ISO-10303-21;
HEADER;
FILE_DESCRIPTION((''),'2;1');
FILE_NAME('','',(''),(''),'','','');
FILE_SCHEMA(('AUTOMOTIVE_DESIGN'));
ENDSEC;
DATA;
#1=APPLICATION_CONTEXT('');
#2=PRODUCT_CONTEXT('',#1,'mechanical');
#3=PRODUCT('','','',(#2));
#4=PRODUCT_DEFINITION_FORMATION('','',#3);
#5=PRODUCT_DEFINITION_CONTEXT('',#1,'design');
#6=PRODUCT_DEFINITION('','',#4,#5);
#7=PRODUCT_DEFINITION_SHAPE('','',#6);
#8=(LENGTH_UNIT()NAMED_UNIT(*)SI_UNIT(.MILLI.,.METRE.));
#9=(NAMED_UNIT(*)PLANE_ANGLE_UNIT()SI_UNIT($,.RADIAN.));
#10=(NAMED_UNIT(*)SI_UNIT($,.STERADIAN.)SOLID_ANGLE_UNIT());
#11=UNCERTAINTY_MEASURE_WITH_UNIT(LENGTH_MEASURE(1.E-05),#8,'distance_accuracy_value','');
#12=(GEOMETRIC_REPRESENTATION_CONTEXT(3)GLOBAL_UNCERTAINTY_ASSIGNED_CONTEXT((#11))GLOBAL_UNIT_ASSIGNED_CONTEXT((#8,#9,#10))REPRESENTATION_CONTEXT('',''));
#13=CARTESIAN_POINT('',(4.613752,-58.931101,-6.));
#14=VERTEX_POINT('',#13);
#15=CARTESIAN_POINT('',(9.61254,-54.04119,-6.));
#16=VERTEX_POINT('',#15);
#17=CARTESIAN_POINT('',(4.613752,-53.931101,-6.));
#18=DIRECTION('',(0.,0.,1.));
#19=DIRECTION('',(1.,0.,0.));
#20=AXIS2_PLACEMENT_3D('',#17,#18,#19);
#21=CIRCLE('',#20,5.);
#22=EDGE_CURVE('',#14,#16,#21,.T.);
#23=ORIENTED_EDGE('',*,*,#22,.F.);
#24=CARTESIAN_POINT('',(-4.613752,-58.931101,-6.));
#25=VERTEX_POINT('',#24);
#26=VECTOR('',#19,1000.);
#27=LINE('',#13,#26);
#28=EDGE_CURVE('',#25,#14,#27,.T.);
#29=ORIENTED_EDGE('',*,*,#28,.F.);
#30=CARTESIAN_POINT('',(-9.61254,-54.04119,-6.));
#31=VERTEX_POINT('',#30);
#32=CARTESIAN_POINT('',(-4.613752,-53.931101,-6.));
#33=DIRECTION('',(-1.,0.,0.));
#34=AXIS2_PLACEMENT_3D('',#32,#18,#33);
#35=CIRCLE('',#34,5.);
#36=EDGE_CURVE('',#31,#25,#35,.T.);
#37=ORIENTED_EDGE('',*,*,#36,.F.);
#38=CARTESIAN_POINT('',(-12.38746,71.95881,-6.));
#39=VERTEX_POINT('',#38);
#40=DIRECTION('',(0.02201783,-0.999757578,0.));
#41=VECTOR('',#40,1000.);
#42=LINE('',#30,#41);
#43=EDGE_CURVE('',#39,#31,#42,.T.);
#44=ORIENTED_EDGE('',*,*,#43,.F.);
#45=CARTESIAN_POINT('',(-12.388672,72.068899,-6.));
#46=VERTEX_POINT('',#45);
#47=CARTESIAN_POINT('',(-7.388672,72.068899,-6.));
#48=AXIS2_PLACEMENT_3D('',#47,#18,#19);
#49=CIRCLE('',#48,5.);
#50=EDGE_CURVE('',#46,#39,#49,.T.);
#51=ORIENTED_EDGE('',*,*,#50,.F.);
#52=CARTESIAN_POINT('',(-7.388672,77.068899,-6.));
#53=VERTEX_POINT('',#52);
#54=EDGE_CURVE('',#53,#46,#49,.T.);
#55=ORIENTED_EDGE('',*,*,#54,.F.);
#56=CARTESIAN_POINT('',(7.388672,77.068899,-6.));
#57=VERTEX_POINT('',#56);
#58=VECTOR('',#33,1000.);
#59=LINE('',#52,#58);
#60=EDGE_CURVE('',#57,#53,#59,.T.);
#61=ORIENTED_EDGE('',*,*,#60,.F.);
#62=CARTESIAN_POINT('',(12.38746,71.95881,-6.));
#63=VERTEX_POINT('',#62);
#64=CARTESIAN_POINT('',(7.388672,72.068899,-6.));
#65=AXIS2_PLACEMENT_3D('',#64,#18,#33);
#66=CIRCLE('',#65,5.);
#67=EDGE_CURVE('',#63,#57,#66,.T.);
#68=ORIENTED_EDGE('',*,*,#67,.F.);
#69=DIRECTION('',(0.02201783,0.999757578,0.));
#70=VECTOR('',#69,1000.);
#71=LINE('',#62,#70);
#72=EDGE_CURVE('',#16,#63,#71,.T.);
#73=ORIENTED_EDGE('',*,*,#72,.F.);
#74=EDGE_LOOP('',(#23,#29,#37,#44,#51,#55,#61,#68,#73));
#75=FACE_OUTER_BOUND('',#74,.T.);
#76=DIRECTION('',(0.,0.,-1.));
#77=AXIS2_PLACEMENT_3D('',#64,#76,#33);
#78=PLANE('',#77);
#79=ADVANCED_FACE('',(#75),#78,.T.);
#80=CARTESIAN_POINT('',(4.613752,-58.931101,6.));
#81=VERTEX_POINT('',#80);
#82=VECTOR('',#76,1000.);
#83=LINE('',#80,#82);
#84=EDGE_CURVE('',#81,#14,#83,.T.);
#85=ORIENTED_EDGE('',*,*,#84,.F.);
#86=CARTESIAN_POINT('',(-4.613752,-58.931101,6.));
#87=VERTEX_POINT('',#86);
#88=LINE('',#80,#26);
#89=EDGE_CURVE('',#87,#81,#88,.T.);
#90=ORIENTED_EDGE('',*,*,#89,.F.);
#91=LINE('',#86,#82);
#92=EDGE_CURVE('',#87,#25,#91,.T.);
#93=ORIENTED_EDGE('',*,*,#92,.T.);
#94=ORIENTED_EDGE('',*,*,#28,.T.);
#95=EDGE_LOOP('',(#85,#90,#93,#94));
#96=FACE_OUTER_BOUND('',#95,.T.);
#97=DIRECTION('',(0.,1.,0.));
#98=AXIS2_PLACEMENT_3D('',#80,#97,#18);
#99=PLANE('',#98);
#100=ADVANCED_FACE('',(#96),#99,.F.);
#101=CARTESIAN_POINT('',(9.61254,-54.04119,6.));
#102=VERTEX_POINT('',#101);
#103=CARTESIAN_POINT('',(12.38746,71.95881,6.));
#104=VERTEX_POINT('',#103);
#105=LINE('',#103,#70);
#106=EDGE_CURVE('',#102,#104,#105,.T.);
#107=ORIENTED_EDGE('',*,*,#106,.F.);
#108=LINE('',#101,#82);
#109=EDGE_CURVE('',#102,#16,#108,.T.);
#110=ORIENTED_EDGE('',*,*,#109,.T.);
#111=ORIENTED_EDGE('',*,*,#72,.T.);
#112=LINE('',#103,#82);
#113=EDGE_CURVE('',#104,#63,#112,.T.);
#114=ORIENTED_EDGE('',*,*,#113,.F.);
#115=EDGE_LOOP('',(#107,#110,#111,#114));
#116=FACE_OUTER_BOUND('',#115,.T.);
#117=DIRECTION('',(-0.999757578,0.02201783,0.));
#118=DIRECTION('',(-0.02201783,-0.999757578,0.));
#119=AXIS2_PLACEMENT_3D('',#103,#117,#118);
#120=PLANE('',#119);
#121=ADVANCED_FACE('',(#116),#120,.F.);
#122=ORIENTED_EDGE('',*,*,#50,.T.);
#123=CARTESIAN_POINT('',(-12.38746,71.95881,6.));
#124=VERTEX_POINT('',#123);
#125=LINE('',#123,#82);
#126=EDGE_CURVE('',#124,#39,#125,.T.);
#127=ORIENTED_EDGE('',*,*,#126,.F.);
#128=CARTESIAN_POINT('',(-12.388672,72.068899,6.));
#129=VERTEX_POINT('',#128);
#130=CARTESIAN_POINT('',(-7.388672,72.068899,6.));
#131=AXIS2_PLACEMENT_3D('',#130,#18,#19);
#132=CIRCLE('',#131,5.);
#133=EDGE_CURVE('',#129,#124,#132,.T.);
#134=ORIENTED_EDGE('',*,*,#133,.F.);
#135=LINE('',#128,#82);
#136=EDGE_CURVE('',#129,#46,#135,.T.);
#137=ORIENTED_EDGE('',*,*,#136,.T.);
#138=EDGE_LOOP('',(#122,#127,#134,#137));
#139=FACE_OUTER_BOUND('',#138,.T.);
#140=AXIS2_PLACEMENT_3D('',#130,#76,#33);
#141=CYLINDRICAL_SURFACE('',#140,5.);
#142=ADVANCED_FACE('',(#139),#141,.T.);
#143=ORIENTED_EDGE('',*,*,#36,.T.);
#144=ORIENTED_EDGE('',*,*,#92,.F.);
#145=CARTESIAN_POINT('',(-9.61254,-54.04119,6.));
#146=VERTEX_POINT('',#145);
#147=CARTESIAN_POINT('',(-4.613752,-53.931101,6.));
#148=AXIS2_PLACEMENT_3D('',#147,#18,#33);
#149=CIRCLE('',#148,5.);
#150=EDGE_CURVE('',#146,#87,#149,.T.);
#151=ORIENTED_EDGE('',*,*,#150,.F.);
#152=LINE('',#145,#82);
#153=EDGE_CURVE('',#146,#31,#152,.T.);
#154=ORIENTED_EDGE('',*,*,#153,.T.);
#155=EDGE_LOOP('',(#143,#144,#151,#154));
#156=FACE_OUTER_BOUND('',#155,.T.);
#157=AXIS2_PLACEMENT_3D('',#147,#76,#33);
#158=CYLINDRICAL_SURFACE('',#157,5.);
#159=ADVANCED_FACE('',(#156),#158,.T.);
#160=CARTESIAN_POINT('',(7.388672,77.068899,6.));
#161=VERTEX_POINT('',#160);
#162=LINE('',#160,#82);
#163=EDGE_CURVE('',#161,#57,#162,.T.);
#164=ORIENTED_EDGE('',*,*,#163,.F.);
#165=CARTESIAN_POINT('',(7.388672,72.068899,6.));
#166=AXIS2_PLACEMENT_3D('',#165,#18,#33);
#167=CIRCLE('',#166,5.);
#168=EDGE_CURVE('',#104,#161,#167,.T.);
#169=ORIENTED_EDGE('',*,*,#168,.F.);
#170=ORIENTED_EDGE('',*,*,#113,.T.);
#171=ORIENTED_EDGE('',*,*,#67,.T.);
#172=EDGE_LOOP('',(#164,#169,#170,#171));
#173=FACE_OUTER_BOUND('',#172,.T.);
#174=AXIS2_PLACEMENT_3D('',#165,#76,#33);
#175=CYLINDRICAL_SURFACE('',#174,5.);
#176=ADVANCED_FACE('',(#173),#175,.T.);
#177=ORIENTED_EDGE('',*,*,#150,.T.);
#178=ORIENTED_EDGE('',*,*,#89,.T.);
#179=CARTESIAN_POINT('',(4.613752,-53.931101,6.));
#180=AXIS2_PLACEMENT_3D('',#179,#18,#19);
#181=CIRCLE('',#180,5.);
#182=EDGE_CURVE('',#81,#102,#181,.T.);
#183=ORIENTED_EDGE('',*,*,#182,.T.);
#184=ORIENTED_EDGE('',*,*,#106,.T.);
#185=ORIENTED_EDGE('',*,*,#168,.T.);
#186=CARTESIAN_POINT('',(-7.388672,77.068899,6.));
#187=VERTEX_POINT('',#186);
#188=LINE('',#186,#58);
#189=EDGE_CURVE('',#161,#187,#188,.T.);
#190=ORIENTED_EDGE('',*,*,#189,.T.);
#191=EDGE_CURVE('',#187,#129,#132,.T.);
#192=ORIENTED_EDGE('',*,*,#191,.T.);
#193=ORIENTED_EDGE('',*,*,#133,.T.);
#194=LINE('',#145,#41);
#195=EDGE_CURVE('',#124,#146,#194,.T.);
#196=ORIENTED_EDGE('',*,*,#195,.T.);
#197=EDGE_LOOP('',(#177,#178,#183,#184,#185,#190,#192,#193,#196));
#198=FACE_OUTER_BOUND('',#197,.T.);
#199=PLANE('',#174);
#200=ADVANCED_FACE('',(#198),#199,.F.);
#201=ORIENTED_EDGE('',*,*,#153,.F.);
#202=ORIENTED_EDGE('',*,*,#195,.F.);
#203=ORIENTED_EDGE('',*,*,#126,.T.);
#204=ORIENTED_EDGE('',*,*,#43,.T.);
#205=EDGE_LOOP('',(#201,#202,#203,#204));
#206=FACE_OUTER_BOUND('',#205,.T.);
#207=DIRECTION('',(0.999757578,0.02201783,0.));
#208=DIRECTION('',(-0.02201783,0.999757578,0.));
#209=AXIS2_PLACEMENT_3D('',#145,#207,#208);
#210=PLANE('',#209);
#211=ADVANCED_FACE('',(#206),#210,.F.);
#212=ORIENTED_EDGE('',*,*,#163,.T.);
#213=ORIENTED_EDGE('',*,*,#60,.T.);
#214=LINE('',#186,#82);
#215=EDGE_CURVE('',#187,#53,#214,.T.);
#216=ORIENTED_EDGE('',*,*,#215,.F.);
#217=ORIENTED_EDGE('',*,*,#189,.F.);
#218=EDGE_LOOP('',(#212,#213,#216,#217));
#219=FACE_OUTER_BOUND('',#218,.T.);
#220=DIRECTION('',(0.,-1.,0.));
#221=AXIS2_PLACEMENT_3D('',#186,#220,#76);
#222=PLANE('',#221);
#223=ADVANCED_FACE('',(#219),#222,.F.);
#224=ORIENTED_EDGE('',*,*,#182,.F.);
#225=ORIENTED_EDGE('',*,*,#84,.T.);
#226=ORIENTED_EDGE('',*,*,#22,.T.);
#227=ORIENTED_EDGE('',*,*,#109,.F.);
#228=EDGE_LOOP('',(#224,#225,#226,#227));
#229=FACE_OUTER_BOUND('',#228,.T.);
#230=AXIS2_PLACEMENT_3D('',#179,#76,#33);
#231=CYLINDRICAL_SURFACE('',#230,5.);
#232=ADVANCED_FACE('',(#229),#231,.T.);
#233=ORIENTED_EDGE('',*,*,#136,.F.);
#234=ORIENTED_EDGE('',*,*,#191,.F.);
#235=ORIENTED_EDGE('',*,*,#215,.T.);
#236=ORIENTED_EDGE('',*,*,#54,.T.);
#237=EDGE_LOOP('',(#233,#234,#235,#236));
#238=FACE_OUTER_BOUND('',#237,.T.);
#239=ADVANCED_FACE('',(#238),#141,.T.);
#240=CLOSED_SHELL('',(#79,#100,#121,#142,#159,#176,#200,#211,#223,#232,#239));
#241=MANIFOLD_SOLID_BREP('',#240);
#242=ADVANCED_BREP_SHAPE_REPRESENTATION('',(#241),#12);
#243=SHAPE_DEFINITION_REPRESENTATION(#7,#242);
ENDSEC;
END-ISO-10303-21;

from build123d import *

# Parameters (mm, degrees)
COTTER_BODY_DEPTH = 6


with BuildPart() as part:
    # Cotter Profile Sketch → Cotter Body (new, symmetric)
    with BuildSketch(Plane.XY):
        with BuildLine():
            Line((-7.388671752, 77.068898934), (7.388671752, 77.068898934))
            ThreePointArc((7.388671752, 77.068898934), (10.962916131, 75.565293809), (12.387459643, 71.958809784))
            Line((12.387459643, 71.958809784), (9.612540357, -54.041190216))
            ThreePointArc((9.612540357, -54.041190216), (8.110147341, -57.505345445), (4.613752466, -58.931101066))
            Line((4.613752466, -58.931101066), (-4.613752466, -58.931101066))
            ThreePointArc((-4.613752466, -58.931101066), (-8.110147341, -57.505345445), (-9.612540357, -54.041190216))
            Line((-9.612540357, -54.041190216), (-12.387459643, 71.958809784))
            ThreePointArc((-12.387459643, 71.958809784), (-10.962916131, 75.565293809), (-7.388671752, 77.068898934))
        make_face()
    extrude(amount=COTTER_BODY_DEPTH, both=True)


solid = part.part
